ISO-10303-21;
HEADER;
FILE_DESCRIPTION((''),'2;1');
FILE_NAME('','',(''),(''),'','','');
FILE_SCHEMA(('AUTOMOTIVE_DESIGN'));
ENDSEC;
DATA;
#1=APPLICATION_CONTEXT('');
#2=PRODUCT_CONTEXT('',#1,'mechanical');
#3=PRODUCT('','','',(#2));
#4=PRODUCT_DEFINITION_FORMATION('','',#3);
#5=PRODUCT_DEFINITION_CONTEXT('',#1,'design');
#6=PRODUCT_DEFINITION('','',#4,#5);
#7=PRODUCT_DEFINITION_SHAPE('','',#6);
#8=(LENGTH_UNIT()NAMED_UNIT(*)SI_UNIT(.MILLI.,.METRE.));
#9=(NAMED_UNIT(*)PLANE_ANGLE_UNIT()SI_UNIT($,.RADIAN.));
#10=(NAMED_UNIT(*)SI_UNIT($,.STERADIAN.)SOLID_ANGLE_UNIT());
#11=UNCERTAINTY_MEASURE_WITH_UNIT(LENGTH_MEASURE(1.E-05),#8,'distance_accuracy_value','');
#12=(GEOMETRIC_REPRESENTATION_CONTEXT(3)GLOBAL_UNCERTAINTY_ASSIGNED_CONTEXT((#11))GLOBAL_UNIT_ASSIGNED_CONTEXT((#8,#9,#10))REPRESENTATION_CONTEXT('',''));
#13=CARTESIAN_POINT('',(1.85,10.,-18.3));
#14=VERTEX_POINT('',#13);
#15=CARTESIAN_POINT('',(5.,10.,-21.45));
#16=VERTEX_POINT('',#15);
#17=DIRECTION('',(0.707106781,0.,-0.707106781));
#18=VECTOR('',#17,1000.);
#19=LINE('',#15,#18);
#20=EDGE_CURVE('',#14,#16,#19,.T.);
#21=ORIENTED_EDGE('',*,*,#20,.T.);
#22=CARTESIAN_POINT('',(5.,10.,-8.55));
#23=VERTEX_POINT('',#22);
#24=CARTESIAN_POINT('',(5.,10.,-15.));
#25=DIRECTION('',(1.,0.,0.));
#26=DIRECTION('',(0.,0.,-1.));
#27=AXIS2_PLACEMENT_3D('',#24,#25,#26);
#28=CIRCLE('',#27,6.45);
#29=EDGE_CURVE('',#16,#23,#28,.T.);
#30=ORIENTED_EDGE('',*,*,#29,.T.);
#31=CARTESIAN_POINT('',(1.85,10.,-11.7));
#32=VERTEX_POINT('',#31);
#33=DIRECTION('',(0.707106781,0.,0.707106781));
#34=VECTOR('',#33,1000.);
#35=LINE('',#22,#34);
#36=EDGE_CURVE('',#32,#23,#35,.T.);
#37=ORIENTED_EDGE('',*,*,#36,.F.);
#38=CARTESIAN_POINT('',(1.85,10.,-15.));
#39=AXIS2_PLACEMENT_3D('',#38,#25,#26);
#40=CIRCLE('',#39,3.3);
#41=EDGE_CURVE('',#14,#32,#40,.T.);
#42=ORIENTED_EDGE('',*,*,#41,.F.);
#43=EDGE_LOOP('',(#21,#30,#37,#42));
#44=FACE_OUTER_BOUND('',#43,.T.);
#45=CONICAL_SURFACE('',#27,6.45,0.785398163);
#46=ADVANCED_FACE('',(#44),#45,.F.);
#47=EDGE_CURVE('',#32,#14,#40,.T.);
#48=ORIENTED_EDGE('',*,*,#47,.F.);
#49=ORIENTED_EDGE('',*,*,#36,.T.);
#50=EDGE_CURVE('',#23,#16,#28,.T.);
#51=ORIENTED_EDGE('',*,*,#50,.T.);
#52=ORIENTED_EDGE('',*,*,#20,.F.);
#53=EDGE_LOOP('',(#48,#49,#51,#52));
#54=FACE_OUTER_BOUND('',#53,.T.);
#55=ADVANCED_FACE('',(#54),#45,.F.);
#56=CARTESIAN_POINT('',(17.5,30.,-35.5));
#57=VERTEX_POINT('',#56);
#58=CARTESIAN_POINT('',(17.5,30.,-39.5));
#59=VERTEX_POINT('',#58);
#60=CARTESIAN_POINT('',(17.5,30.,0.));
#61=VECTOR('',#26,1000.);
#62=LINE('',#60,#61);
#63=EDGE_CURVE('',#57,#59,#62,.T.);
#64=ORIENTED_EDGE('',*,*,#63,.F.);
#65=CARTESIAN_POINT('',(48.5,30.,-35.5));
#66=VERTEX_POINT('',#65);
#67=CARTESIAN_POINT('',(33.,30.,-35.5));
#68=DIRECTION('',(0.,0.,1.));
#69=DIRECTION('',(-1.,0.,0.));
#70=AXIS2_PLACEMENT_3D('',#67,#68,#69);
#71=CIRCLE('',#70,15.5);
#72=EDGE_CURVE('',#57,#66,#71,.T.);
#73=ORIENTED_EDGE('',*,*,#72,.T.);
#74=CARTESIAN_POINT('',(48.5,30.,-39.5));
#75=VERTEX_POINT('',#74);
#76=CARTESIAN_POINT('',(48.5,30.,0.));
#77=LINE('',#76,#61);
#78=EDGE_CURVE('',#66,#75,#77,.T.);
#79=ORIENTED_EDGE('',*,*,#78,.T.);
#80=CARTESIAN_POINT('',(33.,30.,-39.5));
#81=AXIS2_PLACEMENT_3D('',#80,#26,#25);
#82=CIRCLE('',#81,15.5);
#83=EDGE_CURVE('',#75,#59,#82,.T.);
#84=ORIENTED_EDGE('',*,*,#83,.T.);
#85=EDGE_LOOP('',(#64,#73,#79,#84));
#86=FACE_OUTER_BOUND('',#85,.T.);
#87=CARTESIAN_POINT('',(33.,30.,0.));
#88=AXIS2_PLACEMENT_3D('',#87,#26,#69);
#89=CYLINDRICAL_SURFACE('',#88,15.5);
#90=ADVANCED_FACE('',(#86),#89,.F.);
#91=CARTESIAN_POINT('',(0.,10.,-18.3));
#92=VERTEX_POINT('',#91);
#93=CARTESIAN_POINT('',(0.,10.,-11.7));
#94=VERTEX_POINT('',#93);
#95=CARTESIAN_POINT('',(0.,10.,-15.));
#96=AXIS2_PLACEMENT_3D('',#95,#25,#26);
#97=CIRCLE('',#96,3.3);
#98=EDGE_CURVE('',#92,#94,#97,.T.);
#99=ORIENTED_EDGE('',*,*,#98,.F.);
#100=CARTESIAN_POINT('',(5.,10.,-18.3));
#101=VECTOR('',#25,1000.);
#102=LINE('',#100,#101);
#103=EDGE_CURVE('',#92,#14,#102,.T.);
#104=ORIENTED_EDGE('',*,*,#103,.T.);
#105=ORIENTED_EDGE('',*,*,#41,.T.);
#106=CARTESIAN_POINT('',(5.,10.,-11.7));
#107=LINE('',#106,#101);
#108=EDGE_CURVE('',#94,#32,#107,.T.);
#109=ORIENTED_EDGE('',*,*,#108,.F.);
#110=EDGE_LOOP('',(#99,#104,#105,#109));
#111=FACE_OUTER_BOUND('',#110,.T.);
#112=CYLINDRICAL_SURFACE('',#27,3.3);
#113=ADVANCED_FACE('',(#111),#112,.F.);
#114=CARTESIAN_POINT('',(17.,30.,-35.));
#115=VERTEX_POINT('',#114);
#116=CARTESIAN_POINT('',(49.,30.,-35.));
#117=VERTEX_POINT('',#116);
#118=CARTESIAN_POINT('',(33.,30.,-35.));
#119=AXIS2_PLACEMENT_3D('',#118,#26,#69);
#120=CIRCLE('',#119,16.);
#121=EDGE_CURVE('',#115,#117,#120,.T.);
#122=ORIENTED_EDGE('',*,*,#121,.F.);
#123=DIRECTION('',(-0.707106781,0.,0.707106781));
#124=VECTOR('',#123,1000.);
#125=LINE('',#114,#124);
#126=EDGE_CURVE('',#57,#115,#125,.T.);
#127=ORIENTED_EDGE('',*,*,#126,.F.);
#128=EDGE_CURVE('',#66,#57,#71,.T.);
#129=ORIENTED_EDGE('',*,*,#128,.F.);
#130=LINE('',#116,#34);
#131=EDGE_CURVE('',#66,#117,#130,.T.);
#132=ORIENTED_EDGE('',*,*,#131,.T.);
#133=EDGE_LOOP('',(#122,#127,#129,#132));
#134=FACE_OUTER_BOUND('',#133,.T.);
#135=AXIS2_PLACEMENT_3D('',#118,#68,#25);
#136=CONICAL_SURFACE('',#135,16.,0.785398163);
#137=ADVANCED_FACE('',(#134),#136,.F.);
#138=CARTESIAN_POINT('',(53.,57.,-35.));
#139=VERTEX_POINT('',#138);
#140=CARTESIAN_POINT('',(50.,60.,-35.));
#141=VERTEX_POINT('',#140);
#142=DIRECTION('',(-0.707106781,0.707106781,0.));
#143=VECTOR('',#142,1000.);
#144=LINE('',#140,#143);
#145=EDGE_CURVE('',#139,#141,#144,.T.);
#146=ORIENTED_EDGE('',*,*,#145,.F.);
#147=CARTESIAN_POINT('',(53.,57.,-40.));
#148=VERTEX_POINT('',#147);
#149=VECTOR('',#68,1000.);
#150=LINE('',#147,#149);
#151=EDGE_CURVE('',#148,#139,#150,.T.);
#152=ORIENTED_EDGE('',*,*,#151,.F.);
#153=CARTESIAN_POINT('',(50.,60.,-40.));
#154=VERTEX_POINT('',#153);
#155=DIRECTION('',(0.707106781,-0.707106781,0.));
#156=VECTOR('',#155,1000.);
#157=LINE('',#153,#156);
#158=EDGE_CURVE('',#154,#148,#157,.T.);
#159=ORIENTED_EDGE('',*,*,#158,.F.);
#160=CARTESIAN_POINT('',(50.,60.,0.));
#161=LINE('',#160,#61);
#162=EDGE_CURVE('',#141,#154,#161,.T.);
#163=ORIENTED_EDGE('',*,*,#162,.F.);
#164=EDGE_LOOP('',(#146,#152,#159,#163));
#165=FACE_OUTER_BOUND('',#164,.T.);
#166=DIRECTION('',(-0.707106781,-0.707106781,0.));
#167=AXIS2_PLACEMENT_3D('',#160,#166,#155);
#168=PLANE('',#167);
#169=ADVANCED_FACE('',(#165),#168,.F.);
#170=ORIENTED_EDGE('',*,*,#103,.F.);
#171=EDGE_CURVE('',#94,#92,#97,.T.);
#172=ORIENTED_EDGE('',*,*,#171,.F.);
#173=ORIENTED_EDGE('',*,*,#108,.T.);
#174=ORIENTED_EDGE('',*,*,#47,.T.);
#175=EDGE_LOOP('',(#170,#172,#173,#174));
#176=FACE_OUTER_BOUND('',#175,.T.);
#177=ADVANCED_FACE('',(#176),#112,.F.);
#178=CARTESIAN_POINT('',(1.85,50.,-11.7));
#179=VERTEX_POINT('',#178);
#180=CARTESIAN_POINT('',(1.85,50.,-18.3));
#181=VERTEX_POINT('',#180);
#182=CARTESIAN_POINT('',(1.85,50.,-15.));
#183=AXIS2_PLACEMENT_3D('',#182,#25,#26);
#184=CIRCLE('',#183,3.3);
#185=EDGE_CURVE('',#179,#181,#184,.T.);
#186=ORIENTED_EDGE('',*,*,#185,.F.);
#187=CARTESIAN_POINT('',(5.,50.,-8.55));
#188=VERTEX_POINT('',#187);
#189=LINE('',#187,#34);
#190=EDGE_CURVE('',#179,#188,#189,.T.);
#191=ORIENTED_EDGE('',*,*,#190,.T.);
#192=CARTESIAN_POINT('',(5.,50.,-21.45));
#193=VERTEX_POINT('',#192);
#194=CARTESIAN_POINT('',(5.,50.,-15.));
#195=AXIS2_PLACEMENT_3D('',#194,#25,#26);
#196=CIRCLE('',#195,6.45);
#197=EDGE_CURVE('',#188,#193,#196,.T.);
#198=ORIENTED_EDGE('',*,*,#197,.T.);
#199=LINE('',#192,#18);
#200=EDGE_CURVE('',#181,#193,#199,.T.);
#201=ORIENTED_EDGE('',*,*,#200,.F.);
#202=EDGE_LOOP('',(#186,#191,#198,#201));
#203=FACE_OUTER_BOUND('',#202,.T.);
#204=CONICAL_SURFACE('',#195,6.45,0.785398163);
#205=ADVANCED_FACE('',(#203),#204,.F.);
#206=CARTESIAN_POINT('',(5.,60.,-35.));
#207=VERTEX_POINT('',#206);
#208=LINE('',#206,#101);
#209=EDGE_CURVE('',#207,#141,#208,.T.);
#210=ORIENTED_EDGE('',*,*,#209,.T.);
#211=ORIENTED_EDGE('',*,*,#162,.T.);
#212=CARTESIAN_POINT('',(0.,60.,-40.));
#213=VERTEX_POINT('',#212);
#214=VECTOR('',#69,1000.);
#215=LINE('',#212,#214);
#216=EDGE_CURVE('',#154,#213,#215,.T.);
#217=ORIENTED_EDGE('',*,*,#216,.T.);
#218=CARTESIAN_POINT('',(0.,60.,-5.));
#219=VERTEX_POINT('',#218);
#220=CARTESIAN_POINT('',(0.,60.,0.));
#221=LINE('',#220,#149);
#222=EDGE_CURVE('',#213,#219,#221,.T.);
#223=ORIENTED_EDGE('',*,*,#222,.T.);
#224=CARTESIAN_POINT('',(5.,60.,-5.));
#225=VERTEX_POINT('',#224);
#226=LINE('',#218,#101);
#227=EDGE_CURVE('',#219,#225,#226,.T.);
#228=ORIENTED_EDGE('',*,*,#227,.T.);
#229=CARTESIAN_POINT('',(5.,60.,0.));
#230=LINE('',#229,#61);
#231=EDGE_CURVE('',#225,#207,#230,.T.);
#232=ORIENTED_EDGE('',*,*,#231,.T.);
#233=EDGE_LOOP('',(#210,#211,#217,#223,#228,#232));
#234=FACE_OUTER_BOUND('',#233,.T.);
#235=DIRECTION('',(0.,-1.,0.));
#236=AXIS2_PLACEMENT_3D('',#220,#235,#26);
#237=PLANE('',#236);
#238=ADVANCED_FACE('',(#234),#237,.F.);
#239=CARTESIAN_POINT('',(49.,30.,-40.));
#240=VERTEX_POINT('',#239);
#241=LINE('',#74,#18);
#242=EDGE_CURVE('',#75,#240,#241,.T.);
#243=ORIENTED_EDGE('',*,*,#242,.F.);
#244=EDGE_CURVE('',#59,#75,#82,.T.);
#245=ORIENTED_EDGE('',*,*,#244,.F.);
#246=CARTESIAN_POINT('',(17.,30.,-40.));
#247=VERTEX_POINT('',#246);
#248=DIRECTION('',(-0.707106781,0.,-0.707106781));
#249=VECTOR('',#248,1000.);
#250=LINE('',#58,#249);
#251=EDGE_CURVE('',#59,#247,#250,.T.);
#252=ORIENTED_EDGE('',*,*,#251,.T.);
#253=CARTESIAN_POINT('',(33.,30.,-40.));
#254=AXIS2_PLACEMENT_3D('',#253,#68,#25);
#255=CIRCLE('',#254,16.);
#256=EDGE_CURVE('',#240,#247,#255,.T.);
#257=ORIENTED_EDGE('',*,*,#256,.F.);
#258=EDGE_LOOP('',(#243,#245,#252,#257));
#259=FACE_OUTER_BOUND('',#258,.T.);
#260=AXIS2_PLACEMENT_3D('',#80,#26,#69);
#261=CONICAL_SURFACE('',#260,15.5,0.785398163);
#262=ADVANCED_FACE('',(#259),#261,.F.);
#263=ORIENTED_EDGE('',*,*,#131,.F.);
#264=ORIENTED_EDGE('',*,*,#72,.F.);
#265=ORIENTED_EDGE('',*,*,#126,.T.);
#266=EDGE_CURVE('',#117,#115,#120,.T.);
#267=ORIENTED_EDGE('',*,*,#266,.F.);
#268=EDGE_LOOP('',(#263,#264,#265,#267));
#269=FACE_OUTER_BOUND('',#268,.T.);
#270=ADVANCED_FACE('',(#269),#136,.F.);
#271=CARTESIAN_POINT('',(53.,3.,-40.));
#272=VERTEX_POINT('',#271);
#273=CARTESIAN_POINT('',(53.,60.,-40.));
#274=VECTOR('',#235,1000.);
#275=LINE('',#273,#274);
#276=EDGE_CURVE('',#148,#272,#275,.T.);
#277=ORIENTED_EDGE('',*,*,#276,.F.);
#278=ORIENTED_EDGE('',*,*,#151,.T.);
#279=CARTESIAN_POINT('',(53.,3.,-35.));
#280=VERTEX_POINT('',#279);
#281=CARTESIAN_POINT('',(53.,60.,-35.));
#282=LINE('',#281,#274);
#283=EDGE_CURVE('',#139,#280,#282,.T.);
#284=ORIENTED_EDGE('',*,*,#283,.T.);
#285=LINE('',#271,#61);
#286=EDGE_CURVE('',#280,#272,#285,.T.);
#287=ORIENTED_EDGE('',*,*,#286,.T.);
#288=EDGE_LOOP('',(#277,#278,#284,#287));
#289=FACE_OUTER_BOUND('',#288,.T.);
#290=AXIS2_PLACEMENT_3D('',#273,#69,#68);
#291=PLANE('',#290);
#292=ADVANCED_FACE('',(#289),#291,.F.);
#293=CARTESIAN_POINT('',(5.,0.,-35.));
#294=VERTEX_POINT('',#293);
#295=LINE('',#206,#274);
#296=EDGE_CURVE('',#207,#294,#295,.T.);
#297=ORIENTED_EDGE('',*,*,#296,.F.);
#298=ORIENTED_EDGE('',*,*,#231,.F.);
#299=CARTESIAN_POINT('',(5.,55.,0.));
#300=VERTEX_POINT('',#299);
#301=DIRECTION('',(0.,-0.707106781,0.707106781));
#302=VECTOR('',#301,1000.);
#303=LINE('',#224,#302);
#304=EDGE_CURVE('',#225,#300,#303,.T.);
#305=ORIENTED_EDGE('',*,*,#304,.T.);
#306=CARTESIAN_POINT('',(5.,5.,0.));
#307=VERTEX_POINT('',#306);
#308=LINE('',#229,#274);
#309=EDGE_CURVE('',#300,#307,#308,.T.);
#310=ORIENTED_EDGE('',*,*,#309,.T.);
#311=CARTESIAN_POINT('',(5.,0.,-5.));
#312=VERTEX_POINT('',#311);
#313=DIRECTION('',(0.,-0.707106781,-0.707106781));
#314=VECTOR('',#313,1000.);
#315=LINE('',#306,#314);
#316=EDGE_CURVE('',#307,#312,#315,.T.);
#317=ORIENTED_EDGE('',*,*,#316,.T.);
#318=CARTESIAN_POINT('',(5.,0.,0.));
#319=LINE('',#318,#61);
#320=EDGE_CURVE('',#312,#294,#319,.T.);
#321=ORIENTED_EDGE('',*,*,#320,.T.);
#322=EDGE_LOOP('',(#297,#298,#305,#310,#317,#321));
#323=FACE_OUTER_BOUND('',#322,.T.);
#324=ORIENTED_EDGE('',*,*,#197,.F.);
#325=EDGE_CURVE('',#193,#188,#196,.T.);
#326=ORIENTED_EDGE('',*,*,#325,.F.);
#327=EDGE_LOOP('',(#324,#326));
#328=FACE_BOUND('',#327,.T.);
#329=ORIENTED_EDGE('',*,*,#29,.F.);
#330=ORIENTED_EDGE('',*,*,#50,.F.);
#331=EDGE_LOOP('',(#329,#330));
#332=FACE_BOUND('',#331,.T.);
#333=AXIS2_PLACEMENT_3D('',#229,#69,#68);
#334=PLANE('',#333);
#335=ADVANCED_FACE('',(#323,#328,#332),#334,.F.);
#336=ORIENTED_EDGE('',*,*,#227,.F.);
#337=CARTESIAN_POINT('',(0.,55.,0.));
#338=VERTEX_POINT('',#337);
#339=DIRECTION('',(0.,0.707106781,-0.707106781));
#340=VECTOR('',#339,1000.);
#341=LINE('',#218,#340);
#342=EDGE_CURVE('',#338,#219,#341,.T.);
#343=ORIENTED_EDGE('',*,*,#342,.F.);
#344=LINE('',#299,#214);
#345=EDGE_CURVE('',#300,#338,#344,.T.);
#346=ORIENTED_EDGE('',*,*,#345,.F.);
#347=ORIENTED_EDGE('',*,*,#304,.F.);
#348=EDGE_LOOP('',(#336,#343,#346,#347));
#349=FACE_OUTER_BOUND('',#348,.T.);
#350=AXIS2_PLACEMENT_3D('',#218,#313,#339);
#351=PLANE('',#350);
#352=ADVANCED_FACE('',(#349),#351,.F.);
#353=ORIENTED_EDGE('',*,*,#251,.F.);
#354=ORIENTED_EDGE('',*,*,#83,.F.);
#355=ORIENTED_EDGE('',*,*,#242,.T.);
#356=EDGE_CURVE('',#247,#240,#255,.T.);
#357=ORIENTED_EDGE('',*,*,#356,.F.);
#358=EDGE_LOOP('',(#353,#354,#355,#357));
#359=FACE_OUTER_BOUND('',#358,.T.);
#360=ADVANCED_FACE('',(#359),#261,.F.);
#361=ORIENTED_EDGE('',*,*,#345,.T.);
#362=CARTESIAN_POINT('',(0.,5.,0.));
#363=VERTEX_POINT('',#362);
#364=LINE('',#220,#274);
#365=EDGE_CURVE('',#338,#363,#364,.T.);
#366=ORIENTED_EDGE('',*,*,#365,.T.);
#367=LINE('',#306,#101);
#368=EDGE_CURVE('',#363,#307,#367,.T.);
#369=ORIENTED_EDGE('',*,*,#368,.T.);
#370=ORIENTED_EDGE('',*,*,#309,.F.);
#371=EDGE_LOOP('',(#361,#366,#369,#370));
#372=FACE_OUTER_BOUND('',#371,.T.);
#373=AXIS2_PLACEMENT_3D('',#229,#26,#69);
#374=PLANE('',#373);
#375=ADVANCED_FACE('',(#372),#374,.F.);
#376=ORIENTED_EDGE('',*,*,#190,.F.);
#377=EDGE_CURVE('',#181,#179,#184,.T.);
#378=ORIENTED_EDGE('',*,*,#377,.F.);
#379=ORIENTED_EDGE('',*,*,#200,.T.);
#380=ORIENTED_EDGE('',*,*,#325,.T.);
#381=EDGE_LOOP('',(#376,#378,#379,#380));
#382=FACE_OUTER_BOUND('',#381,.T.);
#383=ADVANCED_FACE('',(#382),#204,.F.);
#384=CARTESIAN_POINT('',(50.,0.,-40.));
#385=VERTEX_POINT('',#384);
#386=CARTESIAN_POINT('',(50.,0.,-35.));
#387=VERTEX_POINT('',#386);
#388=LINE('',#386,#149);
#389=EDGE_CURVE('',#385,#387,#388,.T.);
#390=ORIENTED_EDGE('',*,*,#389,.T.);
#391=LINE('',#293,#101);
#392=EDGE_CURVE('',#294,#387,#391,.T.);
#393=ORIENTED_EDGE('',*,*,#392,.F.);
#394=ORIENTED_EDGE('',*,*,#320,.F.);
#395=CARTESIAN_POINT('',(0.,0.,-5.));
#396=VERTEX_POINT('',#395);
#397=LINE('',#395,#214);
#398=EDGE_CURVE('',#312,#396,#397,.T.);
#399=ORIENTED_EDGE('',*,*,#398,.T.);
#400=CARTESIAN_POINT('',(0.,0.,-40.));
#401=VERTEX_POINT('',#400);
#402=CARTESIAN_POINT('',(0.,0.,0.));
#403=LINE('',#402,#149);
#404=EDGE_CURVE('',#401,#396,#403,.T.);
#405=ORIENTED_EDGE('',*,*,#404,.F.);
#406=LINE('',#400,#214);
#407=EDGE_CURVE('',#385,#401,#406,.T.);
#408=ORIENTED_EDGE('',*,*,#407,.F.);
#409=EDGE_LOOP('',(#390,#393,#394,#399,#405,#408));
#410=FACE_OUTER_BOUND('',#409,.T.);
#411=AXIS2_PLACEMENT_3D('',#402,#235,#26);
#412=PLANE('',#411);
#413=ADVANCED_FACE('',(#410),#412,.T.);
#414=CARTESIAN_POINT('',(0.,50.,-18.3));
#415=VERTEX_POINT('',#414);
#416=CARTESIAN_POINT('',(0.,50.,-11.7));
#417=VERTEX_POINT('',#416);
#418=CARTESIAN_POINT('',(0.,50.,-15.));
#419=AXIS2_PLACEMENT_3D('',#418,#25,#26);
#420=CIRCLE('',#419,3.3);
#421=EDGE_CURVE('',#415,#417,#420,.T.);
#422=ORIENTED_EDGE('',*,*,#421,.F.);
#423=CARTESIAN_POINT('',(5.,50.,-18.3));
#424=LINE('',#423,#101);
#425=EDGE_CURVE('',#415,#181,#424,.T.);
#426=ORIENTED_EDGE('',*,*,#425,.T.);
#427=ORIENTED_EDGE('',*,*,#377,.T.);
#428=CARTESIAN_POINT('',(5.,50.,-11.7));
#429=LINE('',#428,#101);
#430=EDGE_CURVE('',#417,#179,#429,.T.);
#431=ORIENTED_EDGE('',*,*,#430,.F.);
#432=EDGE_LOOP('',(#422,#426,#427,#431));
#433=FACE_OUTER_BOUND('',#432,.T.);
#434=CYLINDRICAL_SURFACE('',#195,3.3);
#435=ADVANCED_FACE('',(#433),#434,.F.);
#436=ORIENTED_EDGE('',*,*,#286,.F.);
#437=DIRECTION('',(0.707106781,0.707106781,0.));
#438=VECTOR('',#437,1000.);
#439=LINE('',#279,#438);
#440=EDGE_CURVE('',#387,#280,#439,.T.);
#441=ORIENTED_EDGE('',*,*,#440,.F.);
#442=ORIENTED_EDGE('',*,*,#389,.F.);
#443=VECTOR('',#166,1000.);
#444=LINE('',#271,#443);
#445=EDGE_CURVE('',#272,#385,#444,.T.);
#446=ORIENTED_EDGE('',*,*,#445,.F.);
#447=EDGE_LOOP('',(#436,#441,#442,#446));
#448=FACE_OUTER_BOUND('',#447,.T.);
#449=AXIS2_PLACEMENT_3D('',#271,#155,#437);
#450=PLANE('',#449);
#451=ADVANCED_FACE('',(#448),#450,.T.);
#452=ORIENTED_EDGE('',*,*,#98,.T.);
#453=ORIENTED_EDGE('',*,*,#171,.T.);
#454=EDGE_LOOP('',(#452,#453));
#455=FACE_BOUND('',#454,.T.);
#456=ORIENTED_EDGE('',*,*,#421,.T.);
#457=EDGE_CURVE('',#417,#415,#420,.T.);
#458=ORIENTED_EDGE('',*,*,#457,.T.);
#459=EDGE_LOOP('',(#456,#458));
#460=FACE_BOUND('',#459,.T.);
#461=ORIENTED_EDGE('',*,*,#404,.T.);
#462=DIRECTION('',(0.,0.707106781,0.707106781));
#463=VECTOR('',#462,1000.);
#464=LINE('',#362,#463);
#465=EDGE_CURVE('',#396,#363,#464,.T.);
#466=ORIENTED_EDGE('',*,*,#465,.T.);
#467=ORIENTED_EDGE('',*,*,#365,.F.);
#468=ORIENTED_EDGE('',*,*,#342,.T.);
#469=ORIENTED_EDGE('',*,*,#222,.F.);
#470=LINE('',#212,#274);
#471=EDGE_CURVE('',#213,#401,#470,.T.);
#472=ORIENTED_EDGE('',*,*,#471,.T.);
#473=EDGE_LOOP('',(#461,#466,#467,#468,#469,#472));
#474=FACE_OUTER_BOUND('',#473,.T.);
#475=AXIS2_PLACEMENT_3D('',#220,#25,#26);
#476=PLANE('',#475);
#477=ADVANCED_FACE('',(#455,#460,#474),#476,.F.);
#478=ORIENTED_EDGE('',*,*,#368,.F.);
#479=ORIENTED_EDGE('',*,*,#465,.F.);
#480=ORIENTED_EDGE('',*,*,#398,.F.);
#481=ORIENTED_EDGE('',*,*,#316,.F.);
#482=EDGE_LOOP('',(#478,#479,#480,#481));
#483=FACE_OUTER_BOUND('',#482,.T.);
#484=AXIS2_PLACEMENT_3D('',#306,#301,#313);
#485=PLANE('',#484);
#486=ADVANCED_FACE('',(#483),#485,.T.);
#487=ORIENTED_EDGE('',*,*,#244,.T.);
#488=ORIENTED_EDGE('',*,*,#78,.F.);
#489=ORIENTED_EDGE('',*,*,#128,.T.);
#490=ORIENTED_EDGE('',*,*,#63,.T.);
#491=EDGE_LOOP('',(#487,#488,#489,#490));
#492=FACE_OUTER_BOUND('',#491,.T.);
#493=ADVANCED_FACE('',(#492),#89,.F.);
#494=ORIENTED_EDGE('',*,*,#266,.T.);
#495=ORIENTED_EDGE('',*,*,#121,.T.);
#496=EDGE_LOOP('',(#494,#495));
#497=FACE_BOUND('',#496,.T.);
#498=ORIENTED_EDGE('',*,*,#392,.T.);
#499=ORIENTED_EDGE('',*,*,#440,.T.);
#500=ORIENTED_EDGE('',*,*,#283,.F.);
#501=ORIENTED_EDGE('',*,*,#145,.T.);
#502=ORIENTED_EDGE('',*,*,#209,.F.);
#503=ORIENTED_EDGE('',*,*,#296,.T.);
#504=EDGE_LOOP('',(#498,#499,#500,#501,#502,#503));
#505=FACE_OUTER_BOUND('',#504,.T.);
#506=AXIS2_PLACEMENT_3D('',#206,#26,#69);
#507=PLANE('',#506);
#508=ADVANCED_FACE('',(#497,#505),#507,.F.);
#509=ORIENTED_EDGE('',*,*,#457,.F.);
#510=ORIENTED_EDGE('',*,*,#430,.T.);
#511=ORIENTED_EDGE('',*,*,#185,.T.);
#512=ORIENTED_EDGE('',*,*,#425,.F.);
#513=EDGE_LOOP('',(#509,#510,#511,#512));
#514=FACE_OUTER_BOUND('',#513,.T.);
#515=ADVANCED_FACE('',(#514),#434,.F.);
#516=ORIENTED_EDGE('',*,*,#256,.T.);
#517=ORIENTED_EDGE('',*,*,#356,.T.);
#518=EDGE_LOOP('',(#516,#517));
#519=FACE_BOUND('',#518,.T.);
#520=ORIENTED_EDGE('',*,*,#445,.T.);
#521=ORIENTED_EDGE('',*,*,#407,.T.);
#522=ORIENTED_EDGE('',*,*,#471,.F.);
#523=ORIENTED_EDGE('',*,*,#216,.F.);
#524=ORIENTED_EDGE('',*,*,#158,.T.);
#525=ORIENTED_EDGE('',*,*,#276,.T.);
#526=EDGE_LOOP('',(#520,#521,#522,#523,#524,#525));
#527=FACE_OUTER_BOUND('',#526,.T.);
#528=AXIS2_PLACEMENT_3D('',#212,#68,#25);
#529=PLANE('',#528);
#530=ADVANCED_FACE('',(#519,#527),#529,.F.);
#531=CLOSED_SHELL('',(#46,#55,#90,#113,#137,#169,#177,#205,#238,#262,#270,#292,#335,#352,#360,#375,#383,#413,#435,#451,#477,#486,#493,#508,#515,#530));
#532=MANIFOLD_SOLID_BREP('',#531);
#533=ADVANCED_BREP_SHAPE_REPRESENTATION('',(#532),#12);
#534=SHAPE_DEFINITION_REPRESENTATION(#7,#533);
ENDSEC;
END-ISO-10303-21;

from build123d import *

# Parameters (mm, degrees)
EXTRUDE_1_DEPTH          = 60
SKETCH_2_R               = 15.5
CUT_EXTRUDE_1_DEPTH      = 90.493016487
CHAMFER_1_SIZE           = 3
CHAMFER_2_SIZE           = 5
HOLE_WIZARD_1_AT_2_COUNT = 2
HOLE_WIZARD_1_AT_2_PITCH = 40
CHAMFER_3_SIZE           = 0.5


with BuildPart() as part:
    # 草图1 → 凸台-拉伸1 (new body)
    with BuildSketch(Plane(origin=(0, 0, 0), x_dir=(1, 0, 0), z_dir=(0, 1, 0))):
        Polygon((0, 0), (0, 40), (53, 40), (53, 35), (5, 35), (5, 0), align=None)
    extrude(amount=EXTRUDE_1_DEPTH)

    # 草图2 → 切除-拉伸1 (cut, through all)
    with BuildSketch(Plane(origin=(0, 0, -40), x_dir=(-1, 0, 0), z_dir=(0, 0, -1))):
        with Locations((-33, 30)):
            Circle(SKETCH_2_R)
    extrude(amount=-CUT_EXTRUDE_1_DEPTH, mode=Mode.SUBTRACT)

    # 倒角1
    chamfer_1_edges = [part.edges().sort_by_distance(p)[0] for p in [
        (53, 60, -37.5),
        (53, 0, -37.5),
    ]]
    chamfer(chamfer_1_edges, length=CHAMFER_1_SIZE)

    # 倒角2
    chamfer_2_edges = [part.edges().sort_by_distance(p)[0] for p in [
        (2.5, 60, 0),
        (2.5, 0, 0),
    ]]
    chamfer(chamfer_2_edges, length=CHAMFER_2_SIZE)

    # 草图3 → 打孔尺寸根据十字槽沉头木螺钉的类型1 (revolve, cut)
    with BuildSketch(Plane(origin=(5, 10, -15), x_dir=(0, 0, -1), z_dir=(0, 1, 0))):
        Polygon((0, 0), (0, 5), (3.3, 5), (3.3, 3.15), (6.45, 0), align=None)
    hole_wizard_1 = revolve(axis=Axis((11.35, 10, -15), (-1, 0, 0)), mode=Mode.SUBTRACT)

    # 打孔尺寸根据十字槽沉头木螺钉的类型1 at 2: 打孔尺寸根据十字槽沉头木螺钉的类型1 ×2
    with Locations(*[(0, i * HOLE_WIZARD_1_AT_2_PITCH, 0) for i in range(1, HOLE_WIZARD_1_AT_2_COUNT)]):
        add(hole_wizard_1, mode=Mode.SUBTRACT)

    # 倒角3
    chamfer_3_edges = [part.edges().sort_by_distance(p)[0] for p in [
        (48.5, 30, -35),
        (48.5, 30, -40),
    ]]
    chamfer(chamfer_3_edges, length=CHAMFER_3_SIZE)


solid = part.part
